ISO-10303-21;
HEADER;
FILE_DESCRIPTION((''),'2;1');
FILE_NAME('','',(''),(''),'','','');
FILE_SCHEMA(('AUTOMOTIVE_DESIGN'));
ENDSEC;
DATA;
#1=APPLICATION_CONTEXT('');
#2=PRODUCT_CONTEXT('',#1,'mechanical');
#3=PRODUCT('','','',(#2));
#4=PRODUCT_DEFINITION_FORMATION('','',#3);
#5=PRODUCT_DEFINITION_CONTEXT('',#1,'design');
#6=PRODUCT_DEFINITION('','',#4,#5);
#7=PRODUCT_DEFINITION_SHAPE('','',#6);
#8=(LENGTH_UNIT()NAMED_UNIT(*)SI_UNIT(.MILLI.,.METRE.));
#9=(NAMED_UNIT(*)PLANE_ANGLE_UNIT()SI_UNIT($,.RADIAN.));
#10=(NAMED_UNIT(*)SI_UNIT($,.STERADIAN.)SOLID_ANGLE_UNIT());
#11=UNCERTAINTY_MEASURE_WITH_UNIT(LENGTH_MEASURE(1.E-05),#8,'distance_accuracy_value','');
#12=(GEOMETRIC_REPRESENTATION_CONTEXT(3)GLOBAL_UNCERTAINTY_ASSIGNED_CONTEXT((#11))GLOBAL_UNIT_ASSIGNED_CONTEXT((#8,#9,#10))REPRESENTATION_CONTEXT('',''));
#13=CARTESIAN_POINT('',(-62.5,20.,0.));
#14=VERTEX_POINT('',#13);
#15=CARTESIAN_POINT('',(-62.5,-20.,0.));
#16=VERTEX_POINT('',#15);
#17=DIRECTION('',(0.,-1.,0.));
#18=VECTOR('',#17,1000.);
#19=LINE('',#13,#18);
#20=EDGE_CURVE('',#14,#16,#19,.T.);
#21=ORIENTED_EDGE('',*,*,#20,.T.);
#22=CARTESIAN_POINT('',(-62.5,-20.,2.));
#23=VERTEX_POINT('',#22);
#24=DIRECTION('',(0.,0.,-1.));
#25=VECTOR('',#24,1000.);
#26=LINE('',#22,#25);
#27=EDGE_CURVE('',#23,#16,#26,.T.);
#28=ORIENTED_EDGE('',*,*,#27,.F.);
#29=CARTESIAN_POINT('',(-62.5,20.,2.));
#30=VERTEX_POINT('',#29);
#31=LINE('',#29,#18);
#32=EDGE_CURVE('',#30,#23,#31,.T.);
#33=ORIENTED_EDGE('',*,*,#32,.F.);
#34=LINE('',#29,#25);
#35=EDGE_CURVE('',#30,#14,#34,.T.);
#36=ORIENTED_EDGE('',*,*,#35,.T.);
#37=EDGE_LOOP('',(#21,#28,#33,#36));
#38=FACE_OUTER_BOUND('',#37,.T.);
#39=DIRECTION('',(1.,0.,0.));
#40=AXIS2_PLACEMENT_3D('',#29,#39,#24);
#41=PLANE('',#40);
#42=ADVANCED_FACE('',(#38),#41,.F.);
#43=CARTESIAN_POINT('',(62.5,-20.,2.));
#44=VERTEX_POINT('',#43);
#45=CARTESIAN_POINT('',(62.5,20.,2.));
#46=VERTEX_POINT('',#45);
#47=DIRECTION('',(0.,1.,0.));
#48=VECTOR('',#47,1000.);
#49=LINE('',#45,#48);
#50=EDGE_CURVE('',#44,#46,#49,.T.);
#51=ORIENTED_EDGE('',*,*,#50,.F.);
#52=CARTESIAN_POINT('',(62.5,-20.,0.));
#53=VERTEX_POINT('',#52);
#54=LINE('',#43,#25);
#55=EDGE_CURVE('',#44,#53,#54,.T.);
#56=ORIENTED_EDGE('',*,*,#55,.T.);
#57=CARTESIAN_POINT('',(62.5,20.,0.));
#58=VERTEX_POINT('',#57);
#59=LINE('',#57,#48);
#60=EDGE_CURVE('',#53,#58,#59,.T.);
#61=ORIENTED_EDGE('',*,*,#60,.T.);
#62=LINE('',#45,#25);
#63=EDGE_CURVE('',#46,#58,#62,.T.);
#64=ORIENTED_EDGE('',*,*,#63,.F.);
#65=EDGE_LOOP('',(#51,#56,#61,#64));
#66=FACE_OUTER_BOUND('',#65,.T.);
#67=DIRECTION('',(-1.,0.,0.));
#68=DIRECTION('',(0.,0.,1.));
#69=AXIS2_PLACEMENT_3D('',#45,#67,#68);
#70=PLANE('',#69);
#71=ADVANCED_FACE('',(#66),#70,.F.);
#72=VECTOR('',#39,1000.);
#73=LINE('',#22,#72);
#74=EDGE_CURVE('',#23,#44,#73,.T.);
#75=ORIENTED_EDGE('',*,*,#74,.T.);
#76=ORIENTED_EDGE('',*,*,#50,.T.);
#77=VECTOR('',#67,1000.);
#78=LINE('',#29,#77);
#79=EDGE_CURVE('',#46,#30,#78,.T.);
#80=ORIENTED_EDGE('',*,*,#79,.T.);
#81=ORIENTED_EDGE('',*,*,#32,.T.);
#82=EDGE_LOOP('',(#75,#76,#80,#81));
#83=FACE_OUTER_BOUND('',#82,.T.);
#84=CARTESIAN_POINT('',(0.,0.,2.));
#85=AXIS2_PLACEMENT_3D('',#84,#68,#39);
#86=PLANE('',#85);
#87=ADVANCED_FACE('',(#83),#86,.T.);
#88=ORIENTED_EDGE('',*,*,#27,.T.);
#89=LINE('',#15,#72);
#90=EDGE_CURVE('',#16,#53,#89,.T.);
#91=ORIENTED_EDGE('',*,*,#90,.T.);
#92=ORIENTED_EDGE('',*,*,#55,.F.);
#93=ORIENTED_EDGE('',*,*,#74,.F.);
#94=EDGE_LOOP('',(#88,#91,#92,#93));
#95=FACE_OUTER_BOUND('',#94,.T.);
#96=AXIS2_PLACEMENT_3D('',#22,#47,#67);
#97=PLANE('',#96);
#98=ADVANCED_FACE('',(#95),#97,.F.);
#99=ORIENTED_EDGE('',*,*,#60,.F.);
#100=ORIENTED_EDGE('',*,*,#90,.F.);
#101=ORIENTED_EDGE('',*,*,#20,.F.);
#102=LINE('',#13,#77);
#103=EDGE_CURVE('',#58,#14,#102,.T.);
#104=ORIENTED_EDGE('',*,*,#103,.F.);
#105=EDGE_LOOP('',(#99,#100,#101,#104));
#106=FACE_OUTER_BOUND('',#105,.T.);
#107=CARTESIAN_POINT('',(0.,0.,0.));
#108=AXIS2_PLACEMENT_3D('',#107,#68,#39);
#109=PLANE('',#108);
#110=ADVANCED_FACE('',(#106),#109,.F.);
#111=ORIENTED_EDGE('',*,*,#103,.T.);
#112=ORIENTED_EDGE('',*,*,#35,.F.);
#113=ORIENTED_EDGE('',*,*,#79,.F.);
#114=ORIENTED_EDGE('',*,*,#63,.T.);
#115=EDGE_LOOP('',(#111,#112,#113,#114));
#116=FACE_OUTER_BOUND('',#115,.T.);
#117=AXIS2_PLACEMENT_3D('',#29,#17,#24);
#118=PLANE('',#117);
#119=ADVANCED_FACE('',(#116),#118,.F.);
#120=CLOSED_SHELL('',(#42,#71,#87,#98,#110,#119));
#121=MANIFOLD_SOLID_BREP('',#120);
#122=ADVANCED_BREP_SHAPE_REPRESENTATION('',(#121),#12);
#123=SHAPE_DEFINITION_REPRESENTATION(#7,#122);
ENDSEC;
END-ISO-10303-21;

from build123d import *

# Parameters (mm, degrees)
SKETCH_1_W      = 125
SKETCH_1_H      = 40
EXTRUDE_1_DEPTH = 2


with BuildPart() as part:
    # 草图1 → 凸台-拉伸1 (new body)
    with BuildSketch(Plane.XY):
        Rectangle(SKETCH_1_W, SKETCH_1_H)
    extrude(amount=EXTRUDE_1_DEPTH)


solid = part.part
